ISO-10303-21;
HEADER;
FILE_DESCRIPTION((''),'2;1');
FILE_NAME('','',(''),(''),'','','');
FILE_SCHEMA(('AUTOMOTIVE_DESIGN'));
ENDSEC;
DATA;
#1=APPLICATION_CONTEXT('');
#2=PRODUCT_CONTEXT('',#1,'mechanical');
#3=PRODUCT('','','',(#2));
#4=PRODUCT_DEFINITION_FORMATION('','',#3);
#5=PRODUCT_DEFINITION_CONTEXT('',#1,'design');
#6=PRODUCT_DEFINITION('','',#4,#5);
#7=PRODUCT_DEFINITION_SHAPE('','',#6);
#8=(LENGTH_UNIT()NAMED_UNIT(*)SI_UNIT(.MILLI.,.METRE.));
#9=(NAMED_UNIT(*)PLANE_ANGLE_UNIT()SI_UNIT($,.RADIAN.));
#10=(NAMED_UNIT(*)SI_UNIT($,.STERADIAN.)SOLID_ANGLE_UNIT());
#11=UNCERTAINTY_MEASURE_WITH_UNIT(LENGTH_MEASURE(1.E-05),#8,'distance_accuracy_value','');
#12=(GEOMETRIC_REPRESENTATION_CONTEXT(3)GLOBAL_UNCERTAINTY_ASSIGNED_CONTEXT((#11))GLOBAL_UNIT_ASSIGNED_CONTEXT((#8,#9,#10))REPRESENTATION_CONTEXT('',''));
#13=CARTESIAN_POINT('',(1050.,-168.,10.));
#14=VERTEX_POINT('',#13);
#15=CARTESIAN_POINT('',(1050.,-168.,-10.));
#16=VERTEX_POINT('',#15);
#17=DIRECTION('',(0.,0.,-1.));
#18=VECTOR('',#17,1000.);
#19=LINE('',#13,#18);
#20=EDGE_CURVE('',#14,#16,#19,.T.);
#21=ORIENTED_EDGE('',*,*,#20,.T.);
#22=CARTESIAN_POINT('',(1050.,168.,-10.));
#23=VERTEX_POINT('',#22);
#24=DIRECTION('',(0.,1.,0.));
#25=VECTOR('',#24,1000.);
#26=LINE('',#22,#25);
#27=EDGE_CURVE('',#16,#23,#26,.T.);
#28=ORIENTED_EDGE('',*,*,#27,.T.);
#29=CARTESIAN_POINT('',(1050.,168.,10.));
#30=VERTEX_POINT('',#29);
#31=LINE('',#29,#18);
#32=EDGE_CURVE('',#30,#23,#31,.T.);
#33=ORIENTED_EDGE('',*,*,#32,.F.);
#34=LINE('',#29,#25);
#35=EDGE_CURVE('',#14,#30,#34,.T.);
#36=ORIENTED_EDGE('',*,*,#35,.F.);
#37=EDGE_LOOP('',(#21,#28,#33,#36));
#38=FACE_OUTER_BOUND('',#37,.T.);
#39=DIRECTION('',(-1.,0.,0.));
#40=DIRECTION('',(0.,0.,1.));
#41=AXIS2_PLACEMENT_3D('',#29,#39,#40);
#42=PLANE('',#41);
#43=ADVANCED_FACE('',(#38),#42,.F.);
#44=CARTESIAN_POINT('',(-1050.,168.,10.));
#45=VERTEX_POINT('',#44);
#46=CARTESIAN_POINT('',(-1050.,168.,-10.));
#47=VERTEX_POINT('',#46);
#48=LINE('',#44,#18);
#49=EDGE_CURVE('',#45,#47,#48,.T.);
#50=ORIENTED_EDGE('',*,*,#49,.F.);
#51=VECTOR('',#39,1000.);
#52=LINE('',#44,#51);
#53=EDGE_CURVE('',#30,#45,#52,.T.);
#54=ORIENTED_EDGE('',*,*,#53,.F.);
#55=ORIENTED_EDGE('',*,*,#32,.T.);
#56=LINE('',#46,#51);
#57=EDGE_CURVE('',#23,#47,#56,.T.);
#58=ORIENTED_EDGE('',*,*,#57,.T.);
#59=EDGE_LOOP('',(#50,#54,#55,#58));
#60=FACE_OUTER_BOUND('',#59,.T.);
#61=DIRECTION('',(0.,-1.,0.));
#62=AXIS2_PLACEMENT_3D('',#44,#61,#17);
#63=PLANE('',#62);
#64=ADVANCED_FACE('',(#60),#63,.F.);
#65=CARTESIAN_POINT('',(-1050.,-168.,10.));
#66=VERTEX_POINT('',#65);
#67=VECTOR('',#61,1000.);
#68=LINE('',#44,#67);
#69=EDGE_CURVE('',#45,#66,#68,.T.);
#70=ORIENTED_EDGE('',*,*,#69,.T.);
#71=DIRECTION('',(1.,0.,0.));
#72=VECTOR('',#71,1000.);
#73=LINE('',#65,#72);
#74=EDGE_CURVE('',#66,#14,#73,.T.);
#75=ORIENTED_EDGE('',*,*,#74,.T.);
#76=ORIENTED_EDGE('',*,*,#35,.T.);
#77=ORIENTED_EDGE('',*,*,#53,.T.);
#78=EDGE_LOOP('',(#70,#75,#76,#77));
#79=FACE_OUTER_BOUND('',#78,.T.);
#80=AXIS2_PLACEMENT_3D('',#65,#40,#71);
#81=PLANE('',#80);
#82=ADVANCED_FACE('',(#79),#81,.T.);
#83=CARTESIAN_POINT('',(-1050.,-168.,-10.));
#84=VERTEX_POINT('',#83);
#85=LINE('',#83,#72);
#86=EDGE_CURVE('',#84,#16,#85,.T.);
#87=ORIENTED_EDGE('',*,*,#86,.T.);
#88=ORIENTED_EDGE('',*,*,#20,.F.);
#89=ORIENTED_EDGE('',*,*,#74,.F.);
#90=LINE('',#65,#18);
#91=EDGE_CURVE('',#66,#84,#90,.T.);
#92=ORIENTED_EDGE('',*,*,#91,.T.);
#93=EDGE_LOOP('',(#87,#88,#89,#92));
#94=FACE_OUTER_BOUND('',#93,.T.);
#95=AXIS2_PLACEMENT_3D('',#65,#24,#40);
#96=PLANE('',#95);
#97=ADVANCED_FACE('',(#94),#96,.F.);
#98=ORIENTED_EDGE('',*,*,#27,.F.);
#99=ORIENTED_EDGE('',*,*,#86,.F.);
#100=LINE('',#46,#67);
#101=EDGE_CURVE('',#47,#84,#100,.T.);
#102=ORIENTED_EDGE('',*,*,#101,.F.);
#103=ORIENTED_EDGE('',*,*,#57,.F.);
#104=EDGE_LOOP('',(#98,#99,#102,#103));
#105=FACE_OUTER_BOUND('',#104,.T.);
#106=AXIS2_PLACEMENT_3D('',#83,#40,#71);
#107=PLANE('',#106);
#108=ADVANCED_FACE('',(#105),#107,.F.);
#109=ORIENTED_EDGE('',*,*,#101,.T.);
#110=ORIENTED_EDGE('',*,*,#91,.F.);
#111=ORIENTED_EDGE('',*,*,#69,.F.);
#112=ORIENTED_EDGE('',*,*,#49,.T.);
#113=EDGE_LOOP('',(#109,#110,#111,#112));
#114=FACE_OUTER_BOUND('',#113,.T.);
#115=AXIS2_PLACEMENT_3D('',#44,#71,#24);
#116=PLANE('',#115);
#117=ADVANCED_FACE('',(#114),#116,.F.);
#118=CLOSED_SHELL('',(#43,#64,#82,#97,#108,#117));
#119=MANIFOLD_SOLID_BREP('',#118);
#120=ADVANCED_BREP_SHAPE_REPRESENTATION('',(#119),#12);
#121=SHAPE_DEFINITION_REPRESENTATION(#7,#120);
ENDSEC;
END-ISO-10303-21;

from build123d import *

# Parameters (mm, degrees)
SKETCH1_W           = 2100
SKETCH1_H           = 336
BOSS_EXTRUDE1_DEPTH = 10


with BuildPart() as part:
    # Sketch1 → Boss-Extrude1 (new, symmetric)
    with BuildSketch(Plane.XY):
        Rectangle(SKETCH1_W, SKETCH1_H)
    extrude(amount=BOSS_EXTRUDE1_DEPTH, both=True)


solid = part.part
